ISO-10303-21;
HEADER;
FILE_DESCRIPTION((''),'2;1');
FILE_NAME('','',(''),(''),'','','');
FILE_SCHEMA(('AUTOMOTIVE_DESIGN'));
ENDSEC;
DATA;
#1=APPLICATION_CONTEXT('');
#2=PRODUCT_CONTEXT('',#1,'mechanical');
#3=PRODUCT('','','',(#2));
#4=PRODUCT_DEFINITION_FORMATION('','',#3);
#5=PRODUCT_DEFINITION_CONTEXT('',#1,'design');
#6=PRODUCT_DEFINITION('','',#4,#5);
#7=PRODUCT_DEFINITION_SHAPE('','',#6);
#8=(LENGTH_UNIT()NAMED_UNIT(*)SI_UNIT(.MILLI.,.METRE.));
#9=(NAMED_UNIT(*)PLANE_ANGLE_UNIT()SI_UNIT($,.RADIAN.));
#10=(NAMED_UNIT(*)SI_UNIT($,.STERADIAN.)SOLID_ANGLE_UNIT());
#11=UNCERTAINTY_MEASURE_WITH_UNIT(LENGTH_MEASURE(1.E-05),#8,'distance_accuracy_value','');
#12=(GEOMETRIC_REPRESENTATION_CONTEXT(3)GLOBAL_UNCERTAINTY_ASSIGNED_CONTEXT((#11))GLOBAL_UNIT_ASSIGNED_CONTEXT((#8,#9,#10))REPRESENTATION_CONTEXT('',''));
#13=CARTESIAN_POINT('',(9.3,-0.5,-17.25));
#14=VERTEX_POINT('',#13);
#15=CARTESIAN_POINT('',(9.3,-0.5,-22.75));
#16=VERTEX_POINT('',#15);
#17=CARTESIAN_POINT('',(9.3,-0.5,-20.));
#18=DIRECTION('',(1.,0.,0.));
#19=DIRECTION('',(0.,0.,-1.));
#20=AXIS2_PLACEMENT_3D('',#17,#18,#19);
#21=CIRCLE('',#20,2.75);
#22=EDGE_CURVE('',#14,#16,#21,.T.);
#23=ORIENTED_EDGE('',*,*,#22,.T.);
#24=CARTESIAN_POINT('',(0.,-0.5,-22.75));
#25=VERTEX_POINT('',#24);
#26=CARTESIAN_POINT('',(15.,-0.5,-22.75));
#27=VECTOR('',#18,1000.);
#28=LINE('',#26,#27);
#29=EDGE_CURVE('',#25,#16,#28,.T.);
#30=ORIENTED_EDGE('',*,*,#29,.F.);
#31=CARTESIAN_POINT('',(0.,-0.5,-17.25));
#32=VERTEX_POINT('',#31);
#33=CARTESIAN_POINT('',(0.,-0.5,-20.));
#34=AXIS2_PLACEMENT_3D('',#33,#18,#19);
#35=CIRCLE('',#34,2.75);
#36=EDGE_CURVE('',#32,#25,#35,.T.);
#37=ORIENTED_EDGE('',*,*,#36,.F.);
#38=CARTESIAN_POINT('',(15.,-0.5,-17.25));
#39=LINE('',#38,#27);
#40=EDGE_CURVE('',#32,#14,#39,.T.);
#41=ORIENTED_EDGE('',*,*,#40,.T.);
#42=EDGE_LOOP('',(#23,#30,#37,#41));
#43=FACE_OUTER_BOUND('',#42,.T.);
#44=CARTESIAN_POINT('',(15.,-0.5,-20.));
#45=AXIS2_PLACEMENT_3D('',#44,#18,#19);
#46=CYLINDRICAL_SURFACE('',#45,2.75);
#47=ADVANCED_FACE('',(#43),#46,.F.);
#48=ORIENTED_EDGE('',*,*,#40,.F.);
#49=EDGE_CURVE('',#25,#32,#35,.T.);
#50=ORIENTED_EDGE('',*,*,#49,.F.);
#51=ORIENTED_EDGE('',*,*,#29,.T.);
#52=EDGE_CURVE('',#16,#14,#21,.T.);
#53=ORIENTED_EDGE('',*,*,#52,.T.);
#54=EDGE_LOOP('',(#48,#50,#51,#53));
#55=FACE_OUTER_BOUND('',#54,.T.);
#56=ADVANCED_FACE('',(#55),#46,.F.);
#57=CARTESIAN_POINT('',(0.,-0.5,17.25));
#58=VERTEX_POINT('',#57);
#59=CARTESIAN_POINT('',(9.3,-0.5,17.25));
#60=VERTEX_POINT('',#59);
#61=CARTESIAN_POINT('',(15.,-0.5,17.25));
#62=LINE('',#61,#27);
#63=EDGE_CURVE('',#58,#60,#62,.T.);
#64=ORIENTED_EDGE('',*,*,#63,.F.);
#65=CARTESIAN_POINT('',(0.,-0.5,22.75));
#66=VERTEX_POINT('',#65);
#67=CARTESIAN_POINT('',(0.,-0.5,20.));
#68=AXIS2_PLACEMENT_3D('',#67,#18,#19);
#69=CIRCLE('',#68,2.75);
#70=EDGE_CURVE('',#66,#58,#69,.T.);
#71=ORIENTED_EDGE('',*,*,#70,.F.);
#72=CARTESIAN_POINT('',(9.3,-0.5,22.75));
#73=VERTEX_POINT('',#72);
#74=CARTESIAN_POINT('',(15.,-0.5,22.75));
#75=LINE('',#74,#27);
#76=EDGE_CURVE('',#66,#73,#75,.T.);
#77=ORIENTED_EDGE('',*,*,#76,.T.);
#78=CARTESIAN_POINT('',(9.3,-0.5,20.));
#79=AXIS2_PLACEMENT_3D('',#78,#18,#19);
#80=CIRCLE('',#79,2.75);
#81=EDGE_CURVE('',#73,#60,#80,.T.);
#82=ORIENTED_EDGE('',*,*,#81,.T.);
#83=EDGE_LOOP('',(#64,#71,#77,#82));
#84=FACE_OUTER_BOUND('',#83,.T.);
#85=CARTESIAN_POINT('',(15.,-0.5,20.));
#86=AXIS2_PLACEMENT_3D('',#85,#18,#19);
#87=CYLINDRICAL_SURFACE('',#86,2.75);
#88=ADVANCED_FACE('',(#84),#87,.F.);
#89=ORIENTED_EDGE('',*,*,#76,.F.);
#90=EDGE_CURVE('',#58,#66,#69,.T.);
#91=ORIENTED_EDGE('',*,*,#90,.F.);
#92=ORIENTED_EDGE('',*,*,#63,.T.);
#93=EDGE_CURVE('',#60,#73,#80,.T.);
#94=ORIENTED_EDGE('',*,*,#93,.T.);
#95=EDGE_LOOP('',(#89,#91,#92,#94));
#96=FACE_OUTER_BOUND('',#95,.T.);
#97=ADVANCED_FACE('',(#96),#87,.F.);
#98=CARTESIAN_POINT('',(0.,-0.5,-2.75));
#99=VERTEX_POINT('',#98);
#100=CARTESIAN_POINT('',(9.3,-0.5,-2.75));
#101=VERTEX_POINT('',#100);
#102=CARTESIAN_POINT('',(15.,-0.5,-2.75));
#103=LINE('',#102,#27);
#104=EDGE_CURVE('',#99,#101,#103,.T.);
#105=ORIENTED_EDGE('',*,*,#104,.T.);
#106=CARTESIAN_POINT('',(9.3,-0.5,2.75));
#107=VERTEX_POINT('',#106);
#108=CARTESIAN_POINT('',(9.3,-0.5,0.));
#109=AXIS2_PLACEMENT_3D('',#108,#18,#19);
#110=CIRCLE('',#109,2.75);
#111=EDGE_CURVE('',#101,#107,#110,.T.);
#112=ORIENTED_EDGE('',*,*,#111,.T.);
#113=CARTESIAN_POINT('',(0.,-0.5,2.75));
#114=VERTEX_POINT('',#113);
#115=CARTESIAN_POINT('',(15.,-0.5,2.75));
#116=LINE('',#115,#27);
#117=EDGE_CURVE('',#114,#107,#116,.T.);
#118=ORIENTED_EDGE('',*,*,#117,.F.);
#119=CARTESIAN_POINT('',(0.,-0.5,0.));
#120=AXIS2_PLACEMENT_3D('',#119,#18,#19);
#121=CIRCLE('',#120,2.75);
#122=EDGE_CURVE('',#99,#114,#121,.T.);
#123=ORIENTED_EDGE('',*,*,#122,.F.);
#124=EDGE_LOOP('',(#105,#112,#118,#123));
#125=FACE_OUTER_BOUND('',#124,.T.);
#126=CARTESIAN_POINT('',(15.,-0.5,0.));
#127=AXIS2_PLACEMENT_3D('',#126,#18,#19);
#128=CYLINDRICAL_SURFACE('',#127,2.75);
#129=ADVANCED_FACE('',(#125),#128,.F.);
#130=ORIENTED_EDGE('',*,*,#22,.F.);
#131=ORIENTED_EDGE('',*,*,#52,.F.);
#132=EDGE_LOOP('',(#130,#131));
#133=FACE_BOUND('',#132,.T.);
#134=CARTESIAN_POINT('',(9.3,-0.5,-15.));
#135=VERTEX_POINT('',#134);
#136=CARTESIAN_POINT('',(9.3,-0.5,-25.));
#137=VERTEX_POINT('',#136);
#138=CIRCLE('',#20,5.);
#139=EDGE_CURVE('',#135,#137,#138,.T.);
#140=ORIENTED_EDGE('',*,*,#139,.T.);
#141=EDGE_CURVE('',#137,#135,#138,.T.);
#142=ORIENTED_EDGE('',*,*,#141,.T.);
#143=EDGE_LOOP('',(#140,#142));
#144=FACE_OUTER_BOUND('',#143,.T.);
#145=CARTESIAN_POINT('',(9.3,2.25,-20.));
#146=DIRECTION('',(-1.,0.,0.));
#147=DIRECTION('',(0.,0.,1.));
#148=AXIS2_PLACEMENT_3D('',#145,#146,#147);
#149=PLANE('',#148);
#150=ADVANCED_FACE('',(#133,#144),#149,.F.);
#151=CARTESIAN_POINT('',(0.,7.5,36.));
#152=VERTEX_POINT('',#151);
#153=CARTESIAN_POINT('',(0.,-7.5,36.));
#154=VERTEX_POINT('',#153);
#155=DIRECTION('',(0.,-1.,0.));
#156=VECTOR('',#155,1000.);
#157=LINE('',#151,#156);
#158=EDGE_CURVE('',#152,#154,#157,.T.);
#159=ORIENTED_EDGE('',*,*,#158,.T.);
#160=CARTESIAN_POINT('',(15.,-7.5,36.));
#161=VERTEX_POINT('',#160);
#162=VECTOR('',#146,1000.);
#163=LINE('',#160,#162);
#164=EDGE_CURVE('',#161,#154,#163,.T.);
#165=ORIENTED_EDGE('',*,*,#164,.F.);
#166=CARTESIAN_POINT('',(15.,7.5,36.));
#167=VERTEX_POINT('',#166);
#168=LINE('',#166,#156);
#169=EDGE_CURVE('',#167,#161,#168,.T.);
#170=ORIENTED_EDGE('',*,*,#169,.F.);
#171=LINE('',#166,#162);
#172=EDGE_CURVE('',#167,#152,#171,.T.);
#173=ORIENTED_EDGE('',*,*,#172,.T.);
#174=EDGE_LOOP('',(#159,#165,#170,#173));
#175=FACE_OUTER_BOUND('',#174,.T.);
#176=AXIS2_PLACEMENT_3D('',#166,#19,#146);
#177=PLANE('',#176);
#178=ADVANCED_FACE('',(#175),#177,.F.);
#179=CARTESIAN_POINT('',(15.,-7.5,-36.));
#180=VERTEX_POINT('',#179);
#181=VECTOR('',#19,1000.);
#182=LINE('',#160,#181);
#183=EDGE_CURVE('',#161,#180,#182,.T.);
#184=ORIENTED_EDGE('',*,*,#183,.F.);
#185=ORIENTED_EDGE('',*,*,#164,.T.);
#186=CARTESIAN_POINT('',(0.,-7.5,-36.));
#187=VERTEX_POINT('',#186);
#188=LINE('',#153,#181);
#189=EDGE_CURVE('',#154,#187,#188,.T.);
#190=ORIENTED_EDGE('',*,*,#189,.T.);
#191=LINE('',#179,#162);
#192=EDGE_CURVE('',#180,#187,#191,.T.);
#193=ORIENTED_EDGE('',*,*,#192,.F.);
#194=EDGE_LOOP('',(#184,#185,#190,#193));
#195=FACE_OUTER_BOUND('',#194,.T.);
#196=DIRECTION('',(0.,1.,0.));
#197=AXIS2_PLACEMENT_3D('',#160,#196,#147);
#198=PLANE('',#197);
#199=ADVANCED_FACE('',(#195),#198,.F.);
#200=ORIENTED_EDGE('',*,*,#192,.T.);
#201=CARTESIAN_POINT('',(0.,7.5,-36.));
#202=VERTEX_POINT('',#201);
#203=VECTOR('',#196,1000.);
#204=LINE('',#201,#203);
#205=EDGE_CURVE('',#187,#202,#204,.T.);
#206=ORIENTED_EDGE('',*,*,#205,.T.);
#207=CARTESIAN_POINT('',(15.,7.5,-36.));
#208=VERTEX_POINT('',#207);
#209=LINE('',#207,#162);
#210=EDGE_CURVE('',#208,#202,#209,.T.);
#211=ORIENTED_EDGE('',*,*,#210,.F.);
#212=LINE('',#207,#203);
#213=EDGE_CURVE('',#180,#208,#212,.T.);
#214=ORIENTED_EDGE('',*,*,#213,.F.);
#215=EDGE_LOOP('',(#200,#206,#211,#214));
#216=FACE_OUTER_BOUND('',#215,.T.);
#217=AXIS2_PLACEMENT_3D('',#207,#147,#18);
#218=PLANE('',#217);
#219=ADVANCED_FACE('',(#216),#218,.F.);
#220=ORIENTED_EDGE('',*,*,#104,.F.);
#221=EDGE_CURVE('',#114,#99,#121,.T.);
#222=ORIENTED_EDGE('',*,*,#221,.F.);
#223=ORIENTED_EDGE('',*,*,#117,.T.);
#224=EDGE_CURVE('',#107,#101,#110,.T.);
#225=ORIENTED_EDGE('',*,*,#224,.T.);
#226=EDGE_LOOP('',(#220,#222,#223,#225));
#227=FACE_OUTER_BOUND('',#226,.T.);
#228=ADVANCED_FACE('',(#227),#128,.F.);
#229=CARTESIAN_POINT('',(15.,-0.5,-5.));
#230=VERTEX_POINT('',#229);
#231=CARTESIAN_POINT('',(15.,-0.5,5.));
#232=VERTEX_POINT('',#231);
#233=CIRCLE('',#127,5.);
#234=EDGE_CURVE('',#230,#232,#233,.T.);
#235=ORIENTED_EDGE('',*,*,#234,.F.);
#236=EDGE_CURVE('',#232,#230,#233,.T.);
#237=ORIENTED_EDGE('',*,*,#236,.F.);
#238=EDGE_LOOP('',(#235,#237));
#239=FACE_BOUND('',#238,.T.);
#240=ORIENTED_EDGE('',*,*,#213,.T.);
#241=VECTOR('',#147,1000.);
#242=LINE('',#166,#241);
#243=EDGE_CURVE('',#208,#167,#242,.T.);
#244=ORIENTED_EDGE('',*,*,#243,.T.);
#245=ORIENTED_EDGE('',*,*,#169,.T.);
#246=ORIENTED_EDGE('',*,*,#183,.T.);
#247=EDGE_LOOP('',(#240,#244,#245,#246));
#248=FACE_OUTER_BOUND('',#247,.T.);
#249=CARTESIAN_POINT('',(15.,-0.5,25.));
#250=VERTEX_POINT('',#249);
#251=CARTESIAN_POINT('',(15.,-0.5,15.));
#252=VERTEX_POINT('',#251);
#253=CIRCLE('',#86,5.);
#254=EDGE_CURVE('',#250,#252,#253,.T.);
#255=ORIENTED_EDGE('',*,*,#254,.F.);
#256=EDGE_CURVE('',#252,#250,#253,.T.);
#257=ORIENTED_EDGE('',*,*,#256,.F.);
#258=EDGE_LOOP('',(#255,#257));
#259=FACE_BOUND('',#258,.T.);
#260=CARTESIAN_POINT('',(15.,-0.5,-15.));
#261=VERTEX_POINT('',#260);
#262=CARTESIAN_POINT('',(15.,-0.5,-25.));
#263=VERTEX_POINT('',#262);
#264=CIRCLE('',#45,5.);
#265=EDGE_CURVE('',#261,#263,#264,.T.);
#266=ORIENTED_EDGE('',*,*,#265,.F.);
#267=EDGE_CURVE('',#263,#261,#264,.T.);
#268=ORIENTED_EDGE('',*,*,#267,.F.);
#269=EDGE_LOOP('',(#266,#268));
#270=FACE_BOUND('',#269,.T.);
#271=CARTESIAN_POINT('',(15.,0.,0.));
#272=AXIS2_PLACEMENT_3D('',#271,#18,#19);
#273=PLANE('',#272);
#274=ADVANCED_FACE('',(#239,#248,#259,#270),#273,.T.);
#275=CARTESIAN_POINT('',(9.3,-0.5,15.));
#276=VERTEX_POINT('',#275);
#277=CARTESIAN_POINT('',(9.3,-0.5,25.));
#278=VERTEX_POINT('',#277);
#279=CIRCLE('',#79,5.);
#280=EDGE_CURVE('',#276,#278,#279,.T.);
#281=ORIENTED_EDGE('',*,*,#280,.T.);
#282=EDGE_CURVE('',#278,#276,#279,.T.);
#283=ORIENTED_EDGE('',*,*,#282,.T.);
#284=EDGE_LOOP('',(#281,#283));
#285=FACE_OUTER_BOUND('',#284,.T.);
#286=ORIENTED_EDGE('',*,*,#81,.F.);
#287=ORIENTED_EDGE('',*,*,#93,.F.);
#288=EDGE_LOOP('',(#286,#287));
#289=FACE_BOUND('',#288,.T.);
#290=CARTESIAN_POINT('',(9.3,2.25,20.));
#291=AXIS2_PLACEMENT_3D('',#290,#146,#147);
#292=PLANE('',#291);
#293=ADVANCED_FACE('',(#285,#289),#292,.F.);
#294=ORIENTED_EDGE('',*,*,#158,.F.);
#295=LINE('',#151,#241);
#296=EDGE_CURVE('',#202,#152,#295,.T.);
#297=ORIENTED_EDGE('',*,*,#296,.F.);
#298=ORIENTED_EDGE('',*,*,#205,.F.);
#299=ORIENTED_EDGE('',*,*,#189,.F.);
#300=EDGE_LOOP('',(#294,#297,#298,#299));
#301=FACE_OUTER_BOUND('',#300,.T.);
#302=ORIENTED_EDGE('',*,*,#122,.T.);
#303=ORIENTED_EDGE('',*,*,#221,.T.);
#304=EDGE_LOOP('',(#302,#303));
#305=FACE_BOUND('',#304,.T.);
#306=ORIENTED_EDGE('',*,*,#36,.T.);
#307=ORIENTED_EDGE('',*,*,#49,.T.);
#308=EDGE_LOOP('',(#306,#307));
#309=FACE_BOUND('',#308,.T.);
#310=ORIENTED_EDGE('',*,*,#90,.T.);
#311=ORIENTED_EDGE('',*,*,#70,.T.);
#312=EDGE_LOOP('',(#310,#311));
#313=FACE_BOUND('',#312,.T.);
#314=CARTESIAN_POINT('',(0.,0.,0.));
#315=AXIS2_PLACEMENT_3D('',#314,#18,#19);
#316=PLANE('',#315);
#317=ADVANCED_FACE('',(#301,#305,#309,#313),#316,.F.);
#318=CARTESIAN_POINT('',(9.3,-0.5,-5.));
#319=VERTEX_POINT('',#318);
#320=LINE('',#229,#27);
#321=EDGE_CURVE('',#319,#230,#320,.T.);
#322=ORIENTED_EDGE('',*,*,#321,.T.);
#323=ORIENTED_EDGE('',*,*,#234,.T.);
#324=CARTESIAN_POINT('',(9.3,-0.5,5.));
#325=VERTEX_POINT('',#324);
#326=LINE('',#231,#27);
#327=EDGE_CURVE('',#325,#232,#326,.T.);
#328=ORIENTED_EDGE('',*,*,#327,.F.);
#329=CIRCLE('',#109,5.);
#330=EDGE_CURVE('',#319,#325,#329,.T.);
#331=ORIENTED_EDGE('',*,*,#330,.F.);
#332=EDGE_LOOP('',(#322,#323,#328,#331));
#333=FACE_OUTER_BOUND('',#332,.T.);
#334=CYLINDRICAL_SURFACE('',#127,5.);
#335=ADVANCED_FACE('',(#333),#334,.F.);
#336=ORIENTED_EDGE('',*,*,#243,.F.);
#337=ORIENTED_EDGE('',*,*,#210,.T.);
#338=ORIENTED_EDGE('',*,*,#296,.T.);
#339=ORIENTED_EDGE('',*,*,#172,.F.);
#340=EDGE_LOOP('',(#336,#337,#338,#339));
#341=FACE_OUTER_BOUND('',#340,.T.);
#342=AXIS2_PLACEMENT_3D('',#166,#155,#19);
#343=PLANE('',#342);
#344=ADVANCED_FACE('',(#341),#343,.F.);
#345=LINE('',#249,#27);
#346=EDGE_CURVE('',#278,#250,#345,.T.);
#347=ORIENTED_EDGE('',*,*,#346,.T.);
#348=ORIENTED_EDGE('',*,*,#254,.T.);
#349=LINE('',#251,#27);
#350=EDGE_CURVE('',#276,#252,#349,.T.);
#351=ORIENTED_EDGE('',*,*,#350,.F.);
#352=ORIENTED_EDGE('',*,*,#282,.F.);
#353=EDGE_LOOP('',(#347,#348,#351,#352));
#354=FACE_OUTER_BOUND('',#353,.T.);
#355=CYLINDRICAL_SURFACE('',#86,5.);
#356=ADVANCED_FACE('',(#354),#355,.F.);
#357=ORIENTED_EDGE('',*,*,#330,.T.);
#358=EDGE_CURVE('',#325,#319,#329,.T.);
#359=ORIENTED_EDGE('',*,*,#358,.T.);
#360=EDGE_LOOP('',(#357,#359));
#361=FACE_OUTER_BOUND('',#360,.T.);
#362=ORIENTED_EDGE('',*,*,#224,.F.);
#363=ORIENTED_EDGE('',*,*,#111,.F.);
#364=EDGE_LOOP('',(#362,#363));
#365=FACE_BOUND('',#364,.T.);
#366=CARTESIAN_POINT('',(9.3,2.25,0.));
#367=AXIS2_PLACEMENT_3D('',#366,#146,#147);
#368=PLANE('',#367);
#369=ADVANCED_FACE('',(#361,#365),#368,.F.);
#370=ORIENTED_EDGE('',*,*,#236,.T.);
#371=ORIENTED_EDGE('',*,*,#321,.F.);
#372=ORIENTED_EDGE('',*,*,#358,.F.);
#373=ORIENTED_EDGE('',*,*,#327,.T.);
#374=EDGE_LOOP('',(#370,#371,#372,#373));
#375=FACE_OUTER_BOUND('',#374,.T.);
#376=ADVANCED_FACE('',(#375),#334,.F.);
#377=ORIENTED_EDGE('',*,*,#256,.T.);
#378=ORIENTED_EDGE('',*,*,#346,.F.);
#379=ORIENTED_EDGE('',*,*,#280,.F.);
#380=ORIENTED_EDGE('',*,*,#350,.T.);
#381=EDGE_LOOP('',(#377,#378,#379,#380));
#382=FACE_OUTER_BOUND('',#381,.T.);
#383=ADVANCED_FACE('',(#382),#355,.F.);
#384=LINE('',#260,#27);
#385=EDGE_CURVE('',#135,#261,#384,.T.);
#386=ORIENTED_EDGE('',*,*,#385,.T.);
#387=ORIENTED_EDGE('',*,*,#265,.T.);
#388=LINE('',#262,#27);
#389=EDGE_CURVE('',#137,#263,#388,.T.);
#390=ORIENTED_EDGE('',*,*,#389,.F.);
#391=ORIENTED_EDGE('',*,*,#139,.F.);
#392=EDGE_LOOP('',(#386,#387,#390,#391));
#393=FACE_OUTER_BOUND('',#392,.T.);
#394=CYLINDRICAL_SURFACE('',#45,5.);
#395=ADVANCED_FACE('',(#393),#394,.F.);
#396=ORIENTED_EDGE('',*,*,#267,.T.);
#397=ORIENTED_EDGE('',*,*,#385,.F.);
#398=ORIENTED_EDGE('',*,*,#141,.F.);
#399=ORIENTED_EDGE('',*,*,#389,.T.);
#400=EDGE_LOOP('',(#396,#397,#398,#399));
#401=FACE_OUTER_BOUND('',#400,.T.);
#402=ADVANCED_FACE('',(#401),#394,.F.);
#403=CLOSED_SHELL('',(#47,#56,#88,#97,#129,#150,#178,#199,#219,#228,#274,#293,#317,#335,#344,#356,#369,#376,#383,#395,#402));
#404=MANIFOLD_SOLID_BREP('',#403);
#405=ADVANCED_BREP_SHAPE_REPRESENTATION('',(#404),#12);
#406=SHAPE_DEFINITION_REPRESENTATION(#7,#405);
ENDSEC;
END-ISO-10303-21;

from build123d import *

# Parameters (mm, degrees)
SKETCH_1_W                = 72
SKETCH_1_H                = 15
EXTRUDE_1_DEPTH           = 15
HOLE_WIZARD_2_D           = 5.5
HOLE_WIZARD_2_CBORE_D     = 10
HOLE_WIZARD_2_CBORE_DEPTH = 5.7


with BuildPart() as part:
    # 草图1 → 凸台-拉伸1 (new body)
    with BuildSketch(Plane(origin=(0, 0, 0), x_dir=(0, 0, -1), z_dir=(1, 0, 0))):
        Rectangle(SKETCH_1_W, SKETCH_1_H)
    extrude(amount=EXTRUDE_1_DEPTH)

    # 打孔尺寸(%根据)内六角圆柱头螺钉的类型2 (through all)
    with Locations(Plane(origin=(15, 0, 0), x_dir=(0, 0, -1), z_dir=(1, 0, 0))):
        with Locations((-20, -0.5), (0, -0.5), (20, -0.5)):
            CounterBoreHole(HOLE_WIZARD_2_D / 2, HOLE_WIZARD_2_CBORE_D / 2, HOLE_WIZARD_2_CBORE_DEPTH)


solid = part.part
